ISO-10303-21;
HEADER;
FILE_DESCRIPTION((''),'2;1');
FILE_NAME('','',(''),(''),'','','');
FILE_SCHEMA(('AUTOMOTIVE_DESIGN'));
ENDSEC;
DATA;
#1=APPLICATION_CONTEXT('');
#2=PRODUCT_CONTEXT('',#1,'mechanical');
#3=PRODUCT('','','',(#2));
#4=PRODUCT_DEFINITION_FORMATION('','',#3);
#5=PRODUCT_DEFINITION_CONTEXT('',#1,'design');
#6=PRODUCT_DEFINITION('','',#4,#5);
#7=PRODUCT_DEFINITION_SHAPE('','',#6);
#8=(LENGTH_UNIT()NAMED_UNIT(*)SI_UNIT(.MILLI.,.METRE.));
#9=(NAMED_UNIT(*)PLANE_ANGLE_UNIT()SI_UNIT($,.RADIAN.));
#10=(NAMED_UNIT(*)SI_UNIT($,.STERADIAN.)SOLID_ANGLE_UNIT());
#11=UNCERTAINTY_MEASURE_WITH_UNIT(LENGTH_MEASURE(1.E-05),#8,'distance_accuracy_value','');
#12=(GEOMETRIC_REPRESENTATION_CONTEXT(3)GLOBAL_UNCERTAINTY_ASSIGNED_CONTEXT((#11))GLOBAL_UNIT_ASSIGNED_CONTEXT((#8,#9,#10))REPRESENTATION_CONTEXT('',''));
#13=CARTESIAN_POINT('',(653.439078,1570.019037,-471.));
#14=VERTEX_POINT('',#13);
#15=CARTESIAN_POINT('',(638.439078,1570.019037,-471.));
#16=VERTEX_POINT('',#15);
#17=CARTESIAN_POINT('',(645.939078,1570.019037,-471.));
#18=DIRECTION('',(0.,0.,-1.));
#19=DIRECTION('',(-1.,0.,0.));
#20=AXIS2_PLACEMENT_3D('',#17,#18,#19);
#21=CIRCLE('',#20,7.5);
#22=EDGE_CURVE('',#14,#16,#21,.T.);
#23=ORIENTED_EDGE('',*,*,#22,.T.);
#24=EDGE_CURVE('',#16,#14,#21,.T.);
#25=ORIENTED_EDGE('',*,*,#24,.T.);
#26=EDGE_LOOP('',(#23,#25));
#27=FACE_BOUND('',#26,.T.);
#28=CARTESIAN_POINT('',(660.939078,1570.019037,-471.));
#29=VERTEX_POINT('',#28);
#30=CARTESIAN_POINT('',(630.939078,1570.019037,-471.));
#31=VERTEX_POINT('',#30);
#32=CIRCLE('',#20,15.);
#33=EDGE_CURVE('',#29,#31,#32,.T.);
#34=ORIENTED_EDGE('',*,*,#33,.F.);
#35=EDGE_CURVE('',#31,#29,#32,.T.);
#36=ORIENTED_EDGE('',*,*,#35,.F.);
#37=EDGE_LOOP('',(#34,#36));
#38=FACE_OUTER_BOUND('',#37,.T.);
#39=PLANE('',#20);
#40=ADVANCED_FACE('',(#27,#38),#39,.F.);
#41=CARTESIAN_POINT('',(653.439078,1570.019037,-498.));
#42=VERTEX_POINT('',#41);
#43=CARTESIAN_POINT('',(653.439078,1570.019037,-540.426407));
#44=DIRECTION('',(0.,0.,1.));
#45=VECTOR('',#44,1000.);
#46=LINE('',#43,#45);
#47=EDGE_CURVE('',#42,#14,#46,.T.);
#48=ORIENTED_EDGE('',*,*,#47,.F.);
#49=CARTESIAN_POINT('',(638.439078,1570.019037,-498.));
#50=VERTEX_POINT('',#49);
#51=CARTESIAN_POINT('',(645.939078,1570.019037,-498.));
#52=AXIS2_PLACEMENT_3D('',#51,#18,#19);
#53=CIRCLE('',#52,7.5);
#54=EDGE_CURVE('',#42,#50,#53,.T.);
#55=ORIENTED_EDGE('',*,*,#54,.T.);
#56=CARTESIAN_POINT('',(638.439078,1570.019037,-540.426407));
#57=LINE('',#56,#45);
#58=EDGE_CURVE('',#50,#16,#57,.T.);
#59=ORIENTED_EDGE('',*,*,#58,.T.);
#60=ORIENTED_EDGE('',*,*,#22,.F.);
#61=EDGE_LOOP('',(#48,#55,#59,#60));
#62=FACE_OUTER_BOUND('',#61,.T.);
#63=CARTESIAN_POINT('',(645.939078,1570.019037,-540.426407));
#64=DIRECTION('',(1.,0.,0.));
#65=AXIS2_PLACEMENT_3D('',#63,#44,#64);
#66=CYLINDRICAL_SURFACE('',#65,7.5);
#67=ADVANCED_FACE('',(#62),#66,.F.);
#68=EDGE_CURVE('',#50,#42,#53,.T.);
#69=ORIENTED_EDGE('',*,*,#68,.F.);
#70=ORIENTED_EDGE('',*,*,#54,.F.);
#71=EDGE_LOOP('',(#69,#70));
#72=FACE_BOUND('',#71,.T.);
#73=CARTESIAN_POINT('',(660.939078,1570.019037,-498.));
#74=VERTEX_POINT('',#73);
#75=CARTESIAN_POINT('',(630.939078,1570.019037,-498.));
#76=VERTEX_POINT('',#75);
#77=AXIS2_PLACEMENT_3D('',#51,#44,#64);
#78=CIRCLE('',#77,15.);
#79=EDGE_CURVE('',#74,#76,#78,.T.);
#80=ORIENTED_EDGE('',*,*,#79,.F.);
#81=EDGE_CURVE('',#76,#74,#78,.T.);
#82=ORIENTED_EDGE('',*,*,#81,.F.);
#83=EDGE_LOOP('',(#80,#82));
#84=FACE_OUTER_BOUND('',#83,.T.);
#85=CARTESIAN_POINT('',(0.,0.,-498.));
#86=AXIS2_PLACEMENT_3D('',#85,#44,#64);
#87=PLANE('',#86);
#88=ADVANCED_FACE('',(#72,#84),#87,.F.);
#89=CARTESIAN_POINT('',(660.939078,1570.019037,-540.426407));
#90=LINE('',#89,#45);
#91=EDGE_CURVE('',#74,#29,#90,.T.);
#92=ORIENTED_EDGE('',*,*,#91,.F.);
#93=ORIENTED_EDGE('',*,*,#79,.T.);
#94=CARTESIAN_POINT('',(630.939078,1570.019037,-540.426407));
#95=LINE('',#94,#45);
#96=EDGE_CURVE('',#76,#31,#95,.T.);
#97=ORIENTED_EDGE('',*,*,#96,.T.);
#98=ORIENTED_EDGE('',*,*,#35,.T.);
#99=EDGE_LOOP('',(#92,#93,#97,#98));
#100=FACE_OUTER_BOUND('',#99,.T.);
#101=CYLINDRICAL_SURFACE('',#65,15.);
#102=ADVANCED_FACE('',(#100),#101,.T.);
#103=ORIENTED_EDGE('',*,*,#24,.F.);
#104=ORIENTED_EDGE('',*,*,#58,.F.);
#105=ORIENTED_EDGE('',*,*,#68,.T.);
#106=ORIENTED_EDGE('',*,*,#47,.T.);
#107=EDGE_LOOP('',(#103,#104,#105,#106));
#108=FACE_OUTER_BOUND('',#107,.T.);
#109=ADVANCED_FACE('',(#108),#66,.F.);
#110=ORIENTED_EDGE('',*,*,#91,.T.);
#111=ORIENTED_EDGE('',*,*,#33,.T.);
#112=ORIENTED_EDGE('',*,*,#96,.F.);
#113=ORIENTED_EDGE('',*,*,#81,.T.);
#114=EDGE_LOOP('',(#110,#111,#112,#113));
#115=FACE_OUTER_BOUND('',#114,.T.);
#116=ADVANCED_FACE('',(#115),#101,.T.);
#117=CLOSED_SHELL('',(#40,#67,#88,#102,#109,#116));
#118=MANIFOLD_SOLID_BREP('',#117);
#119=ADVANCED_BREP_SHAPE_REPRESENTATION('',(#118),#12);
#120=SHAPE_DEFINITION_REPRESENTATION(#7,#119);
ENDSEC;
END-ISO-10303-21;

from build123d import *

# Parameters (mm, degrees)
SKETCH_1_R      = 15
SKETCH_1_R_2    = 7.5
EXTRUDE_1_DEPTH = 27


with BuildPart() as part:
    # 草图1 → 凸台-拉伸1 (new body)
    with BuildSketch(Plane(origin=(0, 0, -471), x_dir=(-1, 0, 0), z_dir=(0, 0, -1))):
        with Locations(Location((-645.939078063, 1570.019037425, 0), (0, 0, 180))):
            Circle(SKETCH_1_R)
        with Locations((-645.939078063, 1570.019037425)):
            Circle(SKETCH_1_R_2, mode=Mode.SUBTRACT)
    extrude(amount=EXTRUDE_1_DEPTH)


solid = part.part
